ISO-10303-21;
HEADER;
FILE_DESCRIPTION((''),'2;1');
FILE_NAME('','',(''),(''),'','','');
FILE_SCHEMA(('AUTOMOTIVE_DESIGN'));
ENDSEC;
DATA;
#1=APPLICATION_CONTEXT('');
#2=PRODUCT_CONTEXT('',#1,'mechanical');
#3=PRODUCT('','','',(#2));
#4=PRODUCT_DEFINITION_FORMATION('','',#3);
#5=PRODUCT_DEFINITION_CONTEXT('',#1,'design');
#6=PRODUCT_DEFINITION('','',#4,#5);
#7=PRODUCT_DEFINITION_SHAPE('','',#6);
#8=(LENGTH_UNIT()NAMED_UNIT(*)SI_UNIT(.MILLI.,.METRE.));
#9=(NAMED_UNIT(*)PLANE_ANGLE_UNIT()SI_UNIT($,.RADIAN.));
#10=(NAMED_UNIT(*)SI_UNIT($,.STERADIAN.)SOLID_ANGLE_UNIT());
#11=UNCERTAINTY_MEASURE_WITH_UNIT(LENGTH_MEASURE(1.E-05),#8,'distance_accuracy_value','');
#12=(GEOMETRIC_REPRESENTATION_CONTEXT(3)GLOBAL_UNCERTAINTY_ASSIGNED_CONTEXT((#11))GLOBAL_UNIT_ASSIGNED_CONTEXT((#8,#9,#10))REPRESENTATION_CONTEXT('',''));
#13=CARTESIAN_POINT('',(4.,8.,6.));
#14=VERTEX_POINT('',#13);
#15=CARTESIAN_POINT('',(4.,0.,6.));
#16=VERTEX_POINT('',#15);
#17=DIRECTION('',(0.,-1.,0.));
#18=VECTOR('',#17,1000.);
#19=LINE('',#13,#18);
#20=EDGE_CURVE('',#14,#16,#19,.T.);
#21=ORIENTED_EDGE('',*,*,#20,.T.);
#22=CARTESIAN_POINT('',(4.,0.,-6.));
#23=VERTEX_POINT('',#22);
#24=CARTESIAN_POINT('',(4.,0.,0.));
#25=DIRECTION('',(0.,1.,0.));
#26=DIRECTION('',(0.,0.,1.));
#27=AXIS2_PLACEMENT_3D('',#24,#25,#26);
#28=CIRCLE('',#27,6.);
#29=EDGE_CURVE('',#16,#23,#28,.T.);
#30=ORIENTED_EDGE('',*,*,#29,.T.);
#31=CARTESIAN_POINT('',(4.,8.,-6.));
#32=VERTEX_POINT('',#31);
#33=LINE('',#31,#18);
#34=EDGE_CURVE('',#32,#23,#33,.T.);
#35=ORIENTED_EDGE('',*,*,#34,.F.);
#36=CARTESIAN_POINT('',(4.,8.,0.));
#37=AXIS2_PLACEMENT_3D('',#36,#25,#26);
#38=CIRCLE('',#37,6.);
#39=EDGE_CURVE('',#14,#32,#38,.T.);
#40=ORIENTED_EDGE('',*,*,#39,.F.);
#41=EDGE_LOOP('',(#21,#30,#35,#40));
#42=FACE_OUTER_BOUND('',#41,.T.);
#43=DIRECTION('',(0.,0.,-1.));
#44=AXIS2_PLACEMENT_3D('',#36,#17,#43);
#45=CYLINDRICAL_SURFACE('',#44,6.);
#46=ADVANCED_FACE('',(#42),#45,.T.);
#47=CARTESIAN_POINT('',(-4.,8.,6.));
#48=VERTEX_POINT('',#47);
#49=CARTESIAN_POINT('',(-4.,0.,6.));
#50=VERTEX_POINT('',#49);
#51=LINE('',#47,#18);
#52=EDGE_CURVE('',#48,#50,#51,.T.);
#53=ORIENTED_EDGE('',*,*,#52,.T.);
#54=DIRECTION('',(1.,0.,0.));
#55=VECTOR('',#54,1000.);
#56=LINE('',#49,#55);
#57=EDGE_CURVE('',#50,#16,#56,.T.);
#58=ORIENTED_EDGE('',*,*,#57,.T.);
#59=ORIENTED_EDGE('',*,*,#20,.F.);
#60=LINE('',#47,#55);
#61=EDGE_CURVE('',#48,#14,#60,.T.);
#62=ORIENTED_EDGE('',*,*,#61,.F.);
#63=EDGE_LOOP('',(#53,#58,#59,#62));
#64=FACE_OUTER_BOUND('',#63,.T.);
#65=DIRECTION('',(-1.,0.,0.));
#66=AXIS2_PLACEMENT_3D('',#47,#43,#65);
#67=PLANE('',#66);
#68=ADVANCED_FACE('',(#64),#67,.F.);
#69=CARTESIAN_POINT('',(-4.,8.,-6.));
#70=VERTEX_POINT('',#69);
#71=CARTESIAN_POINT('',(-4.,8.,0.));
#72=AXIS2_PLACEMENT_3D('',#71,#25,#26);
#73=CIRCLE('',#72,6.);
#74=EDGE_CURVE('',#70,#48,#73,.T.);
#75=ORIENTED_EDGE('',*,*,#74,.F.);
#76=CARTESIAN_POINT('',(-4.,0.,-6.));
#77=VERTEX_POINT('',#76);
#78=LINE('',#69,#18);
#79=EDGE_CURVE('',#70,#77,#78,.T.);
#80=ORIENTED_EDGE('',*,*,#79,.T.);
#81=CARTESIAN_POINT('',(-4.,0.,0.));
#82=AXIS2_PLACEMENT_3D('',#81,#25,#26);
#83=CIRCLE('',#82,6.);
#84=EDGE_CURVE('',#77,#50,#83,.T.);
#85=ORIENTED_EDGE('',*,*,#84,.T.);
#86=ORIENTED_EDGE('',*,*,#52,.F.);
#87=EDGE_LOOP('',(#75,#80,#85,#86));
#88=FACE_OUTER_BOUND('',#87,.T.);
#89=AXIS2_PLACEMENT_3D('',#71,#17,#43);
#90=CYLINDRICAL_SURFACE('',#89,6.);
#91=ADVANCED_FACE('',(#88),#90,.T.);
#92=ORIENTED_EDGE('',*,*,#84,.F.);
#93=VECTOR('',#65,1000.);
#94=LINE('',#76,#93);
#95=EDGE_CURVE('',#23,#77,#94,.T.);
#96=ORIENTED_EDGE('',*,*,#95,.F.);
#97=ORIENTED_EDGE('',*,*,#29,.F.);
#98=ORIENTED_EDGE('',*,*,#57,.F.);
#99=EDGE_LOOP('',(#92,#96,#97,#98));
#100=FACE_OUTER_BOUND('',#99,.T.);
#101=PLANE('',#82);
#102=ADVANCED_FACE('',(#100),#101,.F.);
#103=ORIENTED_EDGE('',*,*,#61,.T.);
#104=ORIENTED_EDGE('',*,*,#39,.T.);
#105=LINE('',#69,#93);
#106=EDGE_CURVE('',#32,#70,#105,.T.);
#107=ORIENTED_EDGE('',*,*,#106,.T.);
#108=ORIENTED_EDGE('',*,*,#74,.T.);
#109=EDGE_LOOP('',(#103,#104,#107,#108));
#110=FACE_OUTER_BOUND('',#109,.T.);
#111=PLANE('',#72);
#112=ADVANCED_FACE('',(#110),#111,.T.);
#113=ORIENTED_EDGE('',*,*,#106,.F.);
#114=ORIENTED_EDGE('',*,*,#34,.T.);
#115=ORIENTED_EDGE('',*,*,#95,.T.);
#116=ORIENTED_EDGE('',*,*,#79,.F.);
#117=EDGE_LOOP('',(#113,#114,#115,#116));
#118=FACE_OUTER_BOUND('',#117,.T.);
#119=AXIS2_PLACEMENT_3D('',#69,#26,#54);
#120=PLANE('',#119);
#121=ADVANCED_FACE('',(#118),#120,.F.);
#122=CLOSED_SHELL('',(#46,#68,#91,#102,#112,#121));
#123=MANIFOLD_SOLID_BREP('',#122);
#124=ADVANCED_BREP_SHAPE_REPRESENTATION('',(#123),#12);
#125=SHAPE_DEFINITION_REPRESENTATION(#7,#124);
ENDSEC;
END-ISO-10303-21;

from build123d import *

# Parameters (mm, degrees)
BOSS_EXTRUDE1_DEPTH = 8


with BuildPart() as part:
    # Sketch1 → Boss-Extrude1 (new body)
    with BuildSketch(Plane(origin=(0, 0, 0), x_dir=(1, 0, 0), z_dir=(0, 1, 0))):
        with BuildLine():
            Line((-4, 6), (4, 6))
            ThreePointArc((4, 6), (10, 0), (4, -6))
            Line((4, -6), (-4, -6))
            ThreePointArc((-4, -6), (-10, 0), (-4, 6))
        make_face()
    extrude(amount=BOSS_EXTRUDE1_DEPTH)


solid = part.part
